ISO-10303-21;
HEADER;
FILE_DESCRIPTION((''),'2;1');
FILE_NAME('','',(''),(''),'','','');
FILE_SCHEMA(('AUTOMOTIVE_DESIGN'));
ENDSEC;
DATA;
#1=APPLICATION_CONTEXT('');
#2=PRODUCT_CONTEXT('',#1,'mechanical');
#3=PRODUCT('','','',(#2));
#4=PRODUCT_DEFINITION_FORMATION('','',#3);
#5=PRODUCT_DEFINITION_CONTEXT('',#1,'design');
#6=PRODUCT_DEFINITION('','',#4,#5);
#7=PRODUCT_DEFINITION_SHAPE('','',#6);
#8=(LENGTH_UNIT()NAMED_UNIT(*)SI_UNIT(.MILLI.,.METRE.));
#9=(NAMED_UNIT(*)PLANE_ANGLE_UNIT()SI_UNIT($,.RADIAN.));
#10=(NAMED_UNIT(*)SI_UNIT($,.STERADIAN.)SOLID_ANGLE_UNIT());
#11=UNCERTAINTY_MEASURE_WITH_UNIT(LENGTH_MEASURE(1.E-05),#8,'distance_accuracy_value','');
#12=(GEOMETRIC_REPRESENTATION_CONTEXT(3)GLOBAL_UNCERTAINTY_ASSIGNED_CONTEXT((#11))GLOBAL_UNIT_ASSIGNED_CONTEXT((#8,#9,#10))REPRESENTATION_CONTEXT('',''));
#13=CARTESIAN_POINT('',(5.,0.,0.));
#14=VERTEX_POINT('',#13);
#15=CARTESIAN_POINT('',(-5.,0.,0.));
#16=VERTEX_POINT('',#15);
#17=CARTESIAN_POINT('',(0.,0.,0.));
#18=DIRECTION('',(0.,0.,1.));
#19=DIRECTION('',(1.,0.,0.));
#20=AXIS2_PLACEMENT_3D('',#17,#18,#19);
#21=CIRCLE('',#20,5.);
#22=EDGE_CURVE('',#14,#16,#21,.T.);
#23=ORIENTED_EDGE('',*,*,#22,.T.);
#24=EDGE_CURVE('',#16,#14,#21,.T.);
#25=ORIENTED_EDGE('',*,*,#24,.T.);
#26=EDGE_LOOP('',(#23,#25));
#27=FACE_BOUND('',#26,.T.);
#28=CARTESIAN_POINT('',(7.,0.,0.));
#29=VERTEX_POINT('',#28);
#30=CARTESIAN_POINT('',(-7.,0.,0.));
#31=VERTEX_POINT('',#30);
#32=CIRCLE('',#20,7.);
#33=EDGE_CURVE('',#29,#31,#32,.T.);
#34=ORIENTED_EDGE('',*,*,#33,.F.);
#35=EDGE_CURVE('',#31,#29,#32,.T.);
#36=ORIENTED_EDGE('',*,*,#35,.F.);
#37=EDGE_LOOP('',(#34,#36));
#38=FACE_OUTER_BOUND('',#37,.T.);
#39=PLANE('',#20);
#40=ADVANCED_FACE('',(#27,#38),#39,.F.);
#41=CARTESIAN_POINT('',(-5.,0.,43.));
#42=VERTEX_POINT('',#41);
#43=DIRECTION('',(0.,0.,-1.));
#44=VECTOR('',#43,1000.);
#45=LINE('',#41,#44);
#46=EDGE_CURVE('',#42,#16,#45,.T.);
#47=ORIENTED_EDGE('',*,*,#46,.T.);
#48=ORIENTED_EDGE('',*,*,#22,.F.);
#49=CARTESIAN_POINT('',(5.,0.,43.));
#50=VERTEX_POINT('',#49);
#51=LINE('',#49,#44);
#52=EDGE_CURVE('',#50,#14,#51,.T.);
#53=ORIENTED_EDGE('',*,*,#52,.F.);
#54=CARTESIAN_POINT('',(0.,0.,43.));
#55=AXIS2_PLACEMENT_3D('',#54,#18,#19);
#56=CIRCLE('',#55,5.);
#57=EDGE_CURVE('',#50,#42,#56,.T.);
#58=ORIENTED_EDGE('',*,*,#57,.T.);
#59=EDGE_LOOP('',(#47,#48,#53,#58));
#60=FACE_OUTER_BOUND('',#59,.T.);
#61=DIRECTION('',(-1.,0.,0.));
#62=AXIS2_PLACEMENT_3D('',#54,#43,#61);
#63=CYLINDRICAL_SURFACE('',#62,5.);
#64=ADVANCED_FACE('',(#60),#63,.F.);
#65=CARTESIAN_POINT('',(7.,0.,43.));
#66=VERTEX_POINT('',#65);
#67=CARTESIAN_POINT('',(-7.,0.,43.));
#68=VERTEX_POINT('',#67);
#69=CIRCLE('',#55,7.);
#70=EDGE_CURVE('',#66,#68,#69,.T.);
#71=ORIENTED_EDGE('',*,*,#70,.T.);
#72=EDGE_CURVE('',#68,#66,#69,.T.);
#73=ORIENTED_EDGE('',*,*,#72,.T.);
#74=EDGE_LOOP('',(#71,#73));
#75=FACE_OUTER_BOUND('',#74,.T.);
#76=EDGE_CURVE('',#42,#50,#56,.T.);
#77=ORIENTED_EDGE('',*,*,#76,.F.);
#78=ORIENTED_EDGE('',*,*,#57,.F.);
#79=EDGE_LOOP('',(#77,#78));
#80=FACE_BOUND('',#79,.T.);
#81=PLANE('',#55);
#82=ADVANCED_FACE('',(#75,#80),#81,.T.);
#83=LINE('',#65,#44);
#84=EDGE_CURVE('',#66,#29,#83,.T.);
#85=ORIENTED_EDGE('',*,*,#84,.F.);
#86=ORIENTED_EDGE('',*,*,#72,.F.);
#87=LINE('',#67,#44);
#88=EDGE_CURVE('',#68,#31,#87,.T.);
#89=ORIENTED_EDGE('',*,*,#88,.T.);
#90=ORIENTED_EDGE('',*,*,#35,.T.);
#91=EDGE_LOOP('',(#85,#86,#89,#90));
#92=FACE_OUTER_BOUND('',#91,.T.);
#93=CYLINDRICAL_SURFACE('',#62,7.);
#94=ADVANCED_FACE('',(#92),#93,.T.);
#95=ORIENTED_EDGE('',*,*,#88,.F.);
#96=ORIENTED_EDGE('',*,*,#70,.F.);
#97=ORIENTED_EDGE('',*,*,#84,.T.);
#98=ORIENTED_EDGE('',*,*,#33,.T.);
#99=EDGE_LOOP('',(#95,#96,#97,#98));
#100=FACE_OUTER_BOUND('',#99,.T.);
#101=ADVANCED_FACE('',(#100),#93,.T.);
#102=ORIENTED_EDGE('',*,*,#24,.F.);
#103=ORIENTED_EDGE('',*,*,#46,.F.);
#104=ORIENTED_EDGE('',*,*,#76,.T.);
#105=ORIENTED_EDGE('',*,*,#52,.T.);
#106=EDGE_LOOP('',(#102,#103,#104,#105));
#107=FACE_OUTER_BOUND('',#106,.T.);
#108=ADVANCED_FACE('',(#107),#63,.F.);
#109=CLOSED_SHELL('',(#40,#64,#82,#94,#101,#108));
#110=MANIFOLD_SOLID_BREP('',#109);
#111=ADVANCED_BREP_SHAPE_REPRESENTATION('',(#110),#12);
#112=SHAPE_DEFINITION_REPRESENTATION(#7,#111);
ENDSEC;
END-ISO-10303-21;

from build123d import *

# Parameters (mm, degrees)
SKETCH_1_R      = 7
SKETCH_1_R_2    = 5
EXTRUDE_1_DEPTH = 43


with BuildPart() as part:
    # 草图1 → 凸台-拉伸1 (new body)
    with BuildSketch(Plane.XY):
        Circle(SKETCH_1_R)
        Circle(SKETCH_1_R_2, mode=Mode.SUBTRACT)
    extrude(amount=EXTRUDE_1_DEPTH)


solid = part.part
